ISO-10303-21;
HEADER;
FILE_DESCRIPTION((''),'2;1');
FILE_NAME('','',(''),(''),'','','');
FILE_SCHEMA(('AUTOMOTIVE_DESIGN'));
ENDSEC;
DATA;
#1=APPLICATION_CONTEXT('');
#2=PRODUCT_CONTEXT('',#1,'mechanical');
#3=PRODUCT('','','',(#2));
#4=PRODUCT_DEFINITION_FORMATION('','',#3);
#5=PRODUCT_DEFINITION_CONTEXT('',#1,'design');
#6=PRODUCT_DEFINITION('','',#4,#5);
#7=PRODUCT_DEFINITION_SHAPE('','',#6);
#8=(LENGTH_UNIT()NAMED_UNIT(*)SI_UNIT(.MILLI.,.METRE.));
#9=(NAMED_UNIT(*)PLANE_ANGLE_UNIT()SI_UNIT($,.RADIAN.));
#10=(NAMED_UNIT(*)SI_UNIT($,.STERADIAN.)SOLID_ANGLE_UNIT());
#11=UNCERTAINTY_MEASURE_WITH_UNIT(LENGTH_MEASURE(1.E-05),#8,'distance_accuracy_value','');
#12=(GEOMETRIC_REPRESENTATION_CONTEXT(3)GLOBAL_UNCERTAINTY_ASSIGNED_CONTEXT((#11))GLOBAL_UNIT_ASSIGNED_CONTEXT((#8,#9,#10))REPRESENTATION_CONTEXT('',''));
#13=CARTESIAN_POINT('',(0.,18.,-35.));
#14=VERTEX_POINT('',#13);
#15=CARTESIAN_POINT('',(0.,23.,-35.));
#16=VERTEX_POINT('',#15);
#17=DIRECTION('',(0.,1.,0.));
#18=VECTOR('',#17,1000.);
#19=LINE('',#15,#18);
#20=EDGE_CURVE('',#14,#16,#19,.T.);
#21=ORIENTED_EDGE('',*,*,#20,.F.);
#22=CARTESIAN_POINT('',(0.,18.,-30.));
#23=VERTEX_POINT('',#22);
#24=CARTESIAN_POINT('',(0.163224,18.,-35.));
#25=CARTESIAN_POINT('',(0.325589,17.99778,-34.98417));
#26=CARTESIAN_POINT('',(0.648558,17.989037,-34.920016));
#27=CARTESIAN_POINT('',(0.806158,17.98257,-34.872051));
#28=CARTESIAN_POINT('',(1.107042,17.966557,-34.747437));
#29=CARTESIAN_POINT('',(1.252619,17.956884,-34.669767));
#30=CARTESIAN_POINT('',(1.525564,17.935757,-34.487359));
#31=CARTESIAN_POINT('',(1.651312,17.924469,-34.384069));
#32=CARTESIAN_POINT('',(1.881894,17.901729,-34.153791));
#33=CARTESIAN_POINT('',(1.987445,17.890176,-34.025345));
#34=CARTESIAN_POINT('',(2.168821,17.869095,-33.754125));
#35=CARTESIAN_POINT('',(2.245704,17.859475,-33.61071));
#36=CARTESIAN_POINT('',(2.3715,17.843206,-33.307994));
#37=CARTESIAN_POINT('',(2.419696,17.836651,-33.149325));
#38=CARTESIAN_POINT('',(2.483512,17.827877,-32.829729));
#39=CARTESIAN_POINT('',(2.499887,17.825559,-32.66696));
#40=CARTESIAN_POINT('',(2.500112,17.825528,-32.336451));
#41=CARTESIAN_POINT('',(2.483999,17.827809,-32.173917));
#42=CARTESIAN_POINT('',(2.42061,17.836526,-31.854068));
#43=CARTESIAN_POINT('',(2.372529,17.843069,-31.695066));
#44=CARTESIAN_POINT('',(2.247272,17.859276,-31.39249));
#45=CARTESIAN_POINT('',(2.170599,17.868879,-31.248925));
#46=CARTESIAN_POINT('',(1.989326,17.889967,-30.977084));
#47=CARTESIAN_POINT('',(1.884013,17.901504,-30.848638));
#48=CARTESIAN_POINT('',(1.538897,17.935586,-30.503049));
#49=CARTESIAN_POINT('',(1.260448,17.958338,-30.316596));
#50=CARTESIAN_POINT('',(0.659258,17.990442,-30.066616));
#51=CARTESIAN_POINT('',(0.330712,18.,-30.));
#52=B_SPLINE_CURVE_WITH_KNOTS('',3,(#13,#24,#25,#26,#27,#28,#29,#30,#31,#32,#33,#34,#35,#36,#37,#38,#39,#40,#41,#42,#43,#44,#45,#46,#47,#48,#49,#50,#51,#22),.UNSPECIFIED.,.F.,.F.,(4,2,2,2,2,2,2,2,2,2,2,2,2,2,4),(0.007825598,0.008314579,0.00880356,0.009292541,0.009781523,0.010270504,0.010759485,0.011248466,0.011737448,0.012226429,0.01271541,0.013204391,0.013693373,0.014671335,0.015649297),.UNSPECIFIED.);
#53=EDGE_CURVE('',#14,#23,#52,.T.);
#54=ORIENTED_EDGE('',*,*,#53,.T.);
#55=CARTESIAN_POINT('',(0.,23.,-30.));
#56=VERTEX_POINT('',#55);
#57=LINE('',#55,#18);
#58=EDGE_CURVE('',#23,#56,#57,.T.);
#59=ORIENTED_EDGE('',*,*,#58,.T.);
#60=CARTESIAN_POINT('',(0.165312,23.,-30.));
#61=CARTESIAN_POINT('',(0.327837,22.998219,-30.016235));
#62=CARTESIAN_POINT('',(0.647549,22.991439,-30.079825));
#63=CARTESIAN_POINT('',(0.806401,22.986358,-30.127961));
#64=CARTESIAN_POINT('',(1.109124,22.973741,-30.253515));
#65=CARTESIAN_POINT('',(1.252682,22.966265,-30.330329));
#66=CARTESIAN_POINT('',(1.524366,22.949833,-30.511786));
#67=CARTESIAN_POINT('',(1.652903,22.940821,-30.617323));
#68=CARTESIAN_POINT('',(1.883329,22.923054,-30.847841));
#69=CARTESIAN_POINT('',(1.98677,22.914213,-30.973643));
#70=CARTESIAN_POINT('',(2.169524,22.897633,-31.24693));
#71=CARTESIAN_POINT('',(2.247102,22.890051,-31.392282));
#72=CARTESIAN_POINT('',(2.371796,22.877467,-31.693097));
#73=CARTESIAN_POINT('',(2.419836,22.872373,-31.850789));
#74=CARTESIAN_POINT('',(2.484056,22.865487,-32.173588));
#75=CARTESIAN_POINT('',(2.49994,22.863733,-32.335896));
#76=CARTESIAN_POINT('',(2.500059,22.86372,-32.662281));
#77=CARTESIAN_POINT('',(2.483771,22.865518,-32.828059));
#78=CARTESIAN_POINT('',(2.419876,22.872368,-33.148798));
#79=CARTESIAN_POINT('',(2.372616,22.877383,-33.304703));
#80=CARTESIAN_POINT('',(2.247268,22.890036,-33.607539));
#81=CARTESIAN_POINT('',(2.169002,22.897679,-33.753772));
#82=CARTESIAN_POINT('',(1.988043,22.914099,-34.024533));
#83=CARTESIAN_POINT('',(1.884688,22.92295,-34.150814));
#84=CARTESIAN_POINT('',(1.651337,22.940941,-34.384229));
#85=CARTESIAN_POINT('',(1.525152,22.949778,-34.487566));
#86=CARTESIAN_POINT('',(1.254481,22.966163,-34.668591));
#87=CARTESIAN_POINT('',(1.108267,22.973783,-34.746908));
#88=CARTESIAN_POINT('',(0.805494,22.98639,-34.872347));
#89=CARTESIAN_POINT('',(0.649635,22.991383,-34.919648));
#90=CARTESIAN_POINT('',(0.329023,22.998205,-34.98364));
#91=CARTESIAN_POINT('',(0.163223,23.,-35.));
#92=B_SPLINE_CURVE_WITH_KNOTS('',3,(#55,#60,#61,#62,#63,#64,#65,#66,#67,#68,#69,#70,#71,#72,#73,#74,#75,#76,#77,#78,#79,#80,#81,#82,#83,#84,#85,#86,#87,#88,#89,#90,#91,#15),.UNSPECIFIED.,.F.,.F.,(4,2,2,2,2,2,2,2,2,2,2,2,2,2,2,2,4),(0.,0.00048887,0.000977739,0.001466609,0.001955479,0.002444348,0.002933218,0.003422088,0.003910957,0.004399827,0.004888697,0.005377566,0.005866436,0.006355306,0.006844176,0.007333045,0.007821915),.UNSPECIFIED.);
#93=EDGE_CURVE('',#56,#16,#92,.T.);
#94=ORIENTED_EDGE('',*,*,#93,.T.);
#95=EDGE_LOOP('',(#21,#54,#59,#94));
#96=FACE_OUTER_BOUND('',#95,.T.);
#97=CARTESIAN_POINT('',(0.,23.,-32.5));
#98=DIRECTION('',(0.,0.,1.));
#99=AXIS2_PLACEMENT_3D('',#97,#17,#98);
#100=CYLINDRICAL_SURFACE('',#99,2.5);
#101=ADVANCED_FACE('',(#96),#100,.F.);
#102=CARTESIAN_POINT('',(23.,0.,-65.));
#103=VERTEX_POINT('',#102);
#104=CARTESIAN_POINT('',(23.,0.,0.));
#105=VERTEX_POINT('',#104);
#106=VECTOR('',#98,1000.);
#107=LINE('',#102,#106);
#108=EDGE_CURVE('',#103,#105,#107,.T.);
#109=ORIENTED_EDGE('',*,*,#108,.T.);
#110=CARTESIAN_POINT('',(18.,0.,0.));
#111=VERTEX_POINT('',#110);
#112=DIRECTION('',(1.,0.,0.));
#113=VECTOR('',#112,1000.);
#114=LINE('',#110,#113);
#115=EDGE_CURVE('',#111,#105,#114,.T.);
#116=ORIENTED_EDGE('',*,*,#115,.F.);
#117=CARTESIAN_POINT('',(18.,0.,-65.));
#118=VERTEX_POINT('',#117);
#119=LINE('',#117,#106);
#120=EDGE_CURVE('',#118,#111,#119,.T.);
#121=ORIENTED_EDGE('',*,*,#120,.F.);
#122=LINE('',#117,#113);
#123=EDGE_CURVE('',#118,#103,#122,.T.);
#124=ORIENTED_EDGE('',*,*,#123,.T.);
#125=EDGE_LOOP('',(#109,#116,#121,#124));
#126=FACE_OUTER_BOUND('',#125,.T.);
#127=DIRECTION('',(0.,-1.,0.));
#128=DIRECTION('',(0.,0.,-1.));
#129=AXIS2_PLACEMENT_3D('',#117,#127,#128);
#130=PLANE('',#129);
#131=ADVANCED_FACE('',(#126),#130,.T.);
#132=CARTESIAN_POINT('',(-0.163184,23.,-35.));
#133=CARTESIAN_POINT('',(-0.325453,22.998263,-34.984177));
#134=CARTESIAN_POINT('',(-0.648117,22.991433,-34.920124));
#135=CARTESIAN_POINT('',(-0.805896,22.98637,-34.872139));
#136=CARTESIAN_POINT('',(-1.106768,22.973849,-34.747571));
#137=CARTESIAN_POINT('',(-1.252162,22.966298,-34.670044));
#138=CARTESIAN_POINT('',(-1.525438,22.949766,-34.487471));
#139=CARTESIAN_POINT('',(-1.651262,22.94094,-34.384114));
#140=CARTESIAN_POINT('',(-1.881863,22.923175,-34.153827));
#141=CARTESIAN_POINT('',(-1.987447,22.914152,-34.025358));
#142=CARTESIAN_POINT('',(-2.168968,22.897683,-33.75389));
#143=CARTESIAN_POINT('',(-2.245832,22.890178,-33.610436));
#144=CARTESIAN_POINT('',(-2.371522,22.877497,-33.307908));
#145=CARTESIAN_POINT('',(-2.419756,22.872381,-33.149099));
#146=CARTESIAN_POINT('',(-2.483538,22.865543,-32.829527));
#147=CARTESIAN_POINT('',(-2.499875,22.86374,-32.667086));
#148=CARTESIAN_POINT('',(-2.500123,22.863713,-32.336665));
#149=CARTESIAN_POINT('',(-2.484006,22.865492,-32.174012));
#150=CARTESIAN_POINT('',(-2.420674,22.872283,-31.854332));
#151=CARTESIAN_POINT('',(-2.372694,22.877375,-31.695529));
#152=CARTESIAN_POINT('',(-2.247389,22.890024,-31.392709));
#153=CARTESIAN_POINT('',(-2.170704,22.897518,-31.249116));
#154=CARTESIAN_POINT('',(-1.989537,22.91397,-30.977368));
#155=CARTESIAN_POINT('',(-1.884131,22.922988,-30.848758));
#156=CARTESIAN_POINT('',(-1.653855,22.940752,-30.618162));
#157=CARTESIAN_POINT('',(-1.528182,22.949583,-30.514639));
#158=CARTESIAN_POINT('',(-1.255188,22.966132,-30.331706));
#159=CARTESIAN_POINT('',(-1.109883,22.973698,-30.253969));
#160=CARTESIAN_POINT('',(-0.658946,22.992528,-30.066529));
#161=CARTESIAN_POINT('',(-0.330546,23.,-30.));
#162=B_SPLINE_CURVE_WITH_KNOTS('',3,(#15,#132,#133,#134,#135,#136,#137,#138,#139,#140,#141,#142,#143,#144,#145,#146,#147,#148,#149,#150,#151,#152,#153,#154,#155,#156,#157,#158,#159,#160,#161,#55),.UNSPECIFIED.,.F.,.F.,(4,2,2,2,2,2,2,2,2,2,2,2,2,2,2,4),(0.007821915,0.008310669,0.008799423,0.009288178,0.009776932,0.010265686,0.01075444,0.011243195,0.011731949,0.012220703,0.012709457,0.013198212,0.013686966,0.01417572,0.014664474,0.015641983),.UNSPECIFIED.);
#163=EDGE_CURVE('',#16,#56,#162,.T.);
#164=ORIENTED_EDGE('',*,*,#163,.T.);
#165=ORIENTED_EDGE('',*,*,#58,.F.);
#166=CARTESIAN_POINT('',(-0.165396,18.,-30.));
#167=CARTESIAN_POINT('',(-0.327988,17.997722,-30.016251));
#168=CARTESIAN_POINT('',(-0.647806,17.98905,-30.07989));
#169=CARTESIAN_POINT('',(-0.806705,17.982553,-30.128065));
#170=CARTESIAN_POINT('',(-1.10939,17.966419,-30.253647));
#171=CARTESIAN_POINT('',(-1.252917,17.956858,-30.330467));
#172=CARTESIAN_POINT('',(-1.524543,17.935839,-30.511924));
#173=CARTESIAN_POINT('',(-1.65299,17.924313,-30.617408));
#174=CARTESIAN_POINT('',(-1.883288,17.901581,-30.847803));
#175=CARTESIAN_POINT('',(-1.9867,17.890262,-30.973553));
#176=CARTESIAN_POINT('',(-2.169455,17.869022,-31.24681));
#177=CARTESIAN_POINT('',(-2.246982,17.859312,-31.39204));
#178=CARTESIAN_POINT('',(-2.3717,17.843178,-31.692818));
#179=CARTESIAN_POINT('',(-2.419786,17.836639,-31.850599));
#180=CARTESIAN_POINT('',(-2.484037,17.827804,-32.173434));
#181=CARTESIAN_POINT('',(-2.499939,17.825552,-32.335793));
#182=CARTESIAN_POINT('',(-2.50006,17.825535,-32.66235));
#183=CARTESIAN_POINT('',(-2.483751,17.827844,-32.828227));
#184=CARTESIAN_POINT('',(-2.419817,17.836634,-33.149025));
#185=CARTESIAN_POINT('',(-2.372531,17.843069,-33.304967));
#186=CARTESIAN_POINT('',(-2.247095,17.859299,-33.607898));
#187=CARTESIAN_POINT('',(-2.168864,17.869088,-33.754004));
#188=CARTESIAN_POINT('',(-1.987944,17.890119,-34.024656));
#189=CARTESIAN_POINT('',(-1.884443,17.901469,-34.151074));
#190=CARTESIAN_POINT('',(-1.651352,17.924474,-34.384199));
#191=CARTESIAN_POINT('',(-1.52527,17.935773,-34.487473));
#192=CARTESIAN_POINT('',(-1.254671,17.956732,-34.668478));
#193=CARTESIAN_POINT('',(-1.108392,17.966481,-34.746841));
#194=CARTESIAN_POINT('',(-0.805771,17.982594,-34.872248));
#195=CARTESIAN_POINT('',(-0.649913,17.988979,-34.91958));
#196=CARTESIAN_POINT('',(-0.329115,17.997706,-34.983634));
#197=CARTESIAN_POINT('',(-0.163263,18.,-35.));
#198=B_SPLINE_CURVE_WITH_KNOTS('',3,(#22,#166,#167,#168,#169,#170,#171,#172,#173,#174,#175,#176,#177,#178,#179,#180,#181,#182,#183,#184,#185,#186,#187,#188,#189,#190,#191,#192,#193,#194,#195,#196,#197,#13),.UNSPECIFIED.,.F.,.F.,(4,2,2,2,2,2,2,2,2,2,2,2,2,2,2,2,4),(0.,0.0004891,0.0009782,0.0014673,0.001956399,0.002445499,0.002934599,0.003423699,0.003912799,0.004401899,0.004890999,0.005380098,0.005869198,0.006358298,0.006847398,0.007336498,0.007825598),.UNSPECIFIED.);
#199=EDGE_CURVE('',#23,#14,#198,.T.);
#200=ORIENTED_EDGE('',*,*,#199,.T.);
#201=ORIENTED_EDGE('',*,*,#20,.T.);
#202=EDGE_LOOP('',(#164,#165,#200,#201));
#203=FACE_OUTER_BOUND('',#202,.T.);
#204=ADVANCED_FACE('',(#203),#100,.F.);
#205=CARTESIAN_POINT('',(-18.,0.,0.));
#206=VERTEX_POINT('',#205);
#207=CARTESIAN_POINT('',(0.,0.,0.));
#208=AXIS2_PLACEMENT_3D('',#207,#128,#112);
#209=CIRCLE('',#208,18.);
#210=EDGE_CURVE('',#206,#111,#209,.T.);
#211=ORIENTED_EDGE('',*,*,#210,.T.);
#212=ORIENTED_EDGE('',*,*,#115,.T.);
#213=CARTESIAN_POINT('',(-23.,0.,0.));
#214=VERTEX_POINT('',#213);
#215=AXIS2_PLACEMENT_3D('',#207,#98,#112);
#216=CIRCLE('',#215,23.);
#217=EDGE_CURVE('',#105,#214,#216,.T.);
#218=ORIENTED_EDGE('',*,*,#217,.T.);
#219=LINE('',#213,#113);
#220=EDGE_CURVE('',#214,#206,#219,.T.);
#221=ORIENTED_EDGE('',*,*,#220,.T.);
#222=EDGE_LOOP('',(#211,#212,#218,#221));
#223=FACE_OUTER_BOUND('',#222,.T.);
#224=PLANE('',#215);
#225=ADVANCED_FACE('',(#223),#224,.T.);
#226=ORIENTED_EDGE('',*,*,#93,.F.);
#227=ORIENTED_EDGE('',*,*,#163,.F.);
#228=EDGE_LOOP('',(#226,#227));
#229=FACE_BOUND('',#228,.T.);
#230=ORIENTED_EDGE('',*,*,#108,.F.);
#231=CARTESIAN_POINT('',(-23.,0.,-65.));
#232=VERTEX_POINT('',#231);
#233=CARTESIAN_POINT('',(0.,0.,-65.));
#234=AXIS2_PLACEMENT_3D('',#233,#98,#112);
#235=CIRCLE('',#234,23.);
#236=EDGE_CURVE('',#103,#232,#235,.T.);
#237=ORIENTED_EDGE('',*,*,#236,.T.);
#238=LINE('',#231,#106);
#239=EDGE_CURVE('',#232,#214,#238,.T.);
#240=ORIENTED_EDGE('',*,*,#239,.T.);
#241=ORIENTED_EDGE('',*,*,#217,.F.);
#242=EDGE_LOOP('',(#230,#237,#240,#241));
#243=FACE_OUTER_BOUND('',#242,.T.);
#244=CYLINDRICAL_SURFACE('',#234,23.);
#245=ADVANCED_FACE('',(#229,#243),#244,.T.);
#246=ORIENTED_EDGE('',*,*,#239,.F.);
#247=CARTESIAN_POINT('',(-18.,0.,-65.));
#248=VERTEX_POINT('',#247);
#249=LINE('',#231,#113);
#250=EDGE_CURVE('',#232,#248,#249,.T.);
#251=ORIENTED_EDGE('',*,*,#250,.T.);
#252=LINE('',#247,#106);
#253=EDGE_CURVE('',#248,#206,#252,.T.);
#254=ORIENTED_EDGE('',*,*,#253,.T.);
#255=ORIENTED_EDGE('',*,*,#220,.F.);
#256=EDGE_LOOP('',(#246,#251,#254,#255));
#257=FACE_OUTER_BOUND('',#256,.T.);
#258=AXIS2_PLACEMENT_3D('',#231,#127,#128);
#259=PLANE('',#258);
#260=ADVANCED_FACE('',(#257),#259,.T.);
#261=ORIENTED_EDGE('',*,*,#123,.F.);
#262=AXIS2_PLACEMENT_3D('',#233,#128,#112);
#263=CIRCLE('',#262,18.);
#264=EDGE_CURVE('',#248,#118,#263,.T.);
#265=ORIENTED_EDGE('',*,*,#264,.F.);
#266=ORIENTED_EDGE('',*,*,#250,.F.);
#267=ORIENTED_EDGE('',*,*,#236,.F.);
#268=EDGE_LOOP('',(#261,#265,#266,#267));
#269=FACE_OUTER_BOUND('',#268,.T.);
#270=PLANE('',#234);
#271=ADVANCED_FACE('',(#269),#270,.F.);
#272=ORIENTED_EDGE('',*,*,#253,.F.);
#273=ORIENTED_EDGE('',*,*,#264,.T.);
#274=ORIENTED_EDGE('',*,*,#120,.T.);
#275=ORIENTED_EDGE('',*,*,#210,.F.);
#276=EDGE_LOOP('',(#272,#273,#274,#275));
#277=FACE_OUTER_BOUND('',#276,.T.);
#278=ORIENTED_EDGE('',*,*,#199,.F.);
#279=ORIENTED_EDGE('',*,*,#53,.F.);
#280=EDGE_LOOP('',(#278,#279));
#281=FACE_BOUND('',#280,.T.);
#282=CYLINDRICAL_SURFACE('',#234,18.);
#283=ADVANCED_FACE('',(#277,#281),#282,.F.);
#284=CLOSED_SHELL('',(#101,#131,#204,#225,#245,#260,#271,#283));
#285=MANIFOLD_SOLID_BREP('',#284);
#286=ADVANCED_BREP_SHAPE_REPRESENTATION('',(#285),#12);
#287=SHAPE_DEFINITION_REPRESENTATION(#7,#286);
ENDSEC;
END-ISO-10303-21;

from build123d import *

# Parameters (mm, degrees)
EXTRUDE_1_DEPTH    = 65
HOLE_WIZARD_M6_1_D = 5


with BuildPart() as part:
    # 草图1 → 凸台-拉伸1 (new body)
    with BuildSketch(Plane.XY):
        with BuildLine():
            Line((-23, 0), (-18, 0))
            ThreePointArc((-18, 0), (0, 18), (18, 0))
            Line((18, 0), (23, 0))
            ThreePointArc((23, 0), (0, 23), (-23, 0))
        make_face()
    extrude(amount=-EXTRUDE_1_DEPTH)

    # M6 螺纹孔1 (through all)
    with Locations(Plane(origin=(0, 23, -32.5), x_dir=(1, 0, 0), z_dir=(0, 1, 0))):
        with Locations((0, 0)):
            Hole(HOLE_WIZARD_M6_1_D / 2)


solid = part.part
